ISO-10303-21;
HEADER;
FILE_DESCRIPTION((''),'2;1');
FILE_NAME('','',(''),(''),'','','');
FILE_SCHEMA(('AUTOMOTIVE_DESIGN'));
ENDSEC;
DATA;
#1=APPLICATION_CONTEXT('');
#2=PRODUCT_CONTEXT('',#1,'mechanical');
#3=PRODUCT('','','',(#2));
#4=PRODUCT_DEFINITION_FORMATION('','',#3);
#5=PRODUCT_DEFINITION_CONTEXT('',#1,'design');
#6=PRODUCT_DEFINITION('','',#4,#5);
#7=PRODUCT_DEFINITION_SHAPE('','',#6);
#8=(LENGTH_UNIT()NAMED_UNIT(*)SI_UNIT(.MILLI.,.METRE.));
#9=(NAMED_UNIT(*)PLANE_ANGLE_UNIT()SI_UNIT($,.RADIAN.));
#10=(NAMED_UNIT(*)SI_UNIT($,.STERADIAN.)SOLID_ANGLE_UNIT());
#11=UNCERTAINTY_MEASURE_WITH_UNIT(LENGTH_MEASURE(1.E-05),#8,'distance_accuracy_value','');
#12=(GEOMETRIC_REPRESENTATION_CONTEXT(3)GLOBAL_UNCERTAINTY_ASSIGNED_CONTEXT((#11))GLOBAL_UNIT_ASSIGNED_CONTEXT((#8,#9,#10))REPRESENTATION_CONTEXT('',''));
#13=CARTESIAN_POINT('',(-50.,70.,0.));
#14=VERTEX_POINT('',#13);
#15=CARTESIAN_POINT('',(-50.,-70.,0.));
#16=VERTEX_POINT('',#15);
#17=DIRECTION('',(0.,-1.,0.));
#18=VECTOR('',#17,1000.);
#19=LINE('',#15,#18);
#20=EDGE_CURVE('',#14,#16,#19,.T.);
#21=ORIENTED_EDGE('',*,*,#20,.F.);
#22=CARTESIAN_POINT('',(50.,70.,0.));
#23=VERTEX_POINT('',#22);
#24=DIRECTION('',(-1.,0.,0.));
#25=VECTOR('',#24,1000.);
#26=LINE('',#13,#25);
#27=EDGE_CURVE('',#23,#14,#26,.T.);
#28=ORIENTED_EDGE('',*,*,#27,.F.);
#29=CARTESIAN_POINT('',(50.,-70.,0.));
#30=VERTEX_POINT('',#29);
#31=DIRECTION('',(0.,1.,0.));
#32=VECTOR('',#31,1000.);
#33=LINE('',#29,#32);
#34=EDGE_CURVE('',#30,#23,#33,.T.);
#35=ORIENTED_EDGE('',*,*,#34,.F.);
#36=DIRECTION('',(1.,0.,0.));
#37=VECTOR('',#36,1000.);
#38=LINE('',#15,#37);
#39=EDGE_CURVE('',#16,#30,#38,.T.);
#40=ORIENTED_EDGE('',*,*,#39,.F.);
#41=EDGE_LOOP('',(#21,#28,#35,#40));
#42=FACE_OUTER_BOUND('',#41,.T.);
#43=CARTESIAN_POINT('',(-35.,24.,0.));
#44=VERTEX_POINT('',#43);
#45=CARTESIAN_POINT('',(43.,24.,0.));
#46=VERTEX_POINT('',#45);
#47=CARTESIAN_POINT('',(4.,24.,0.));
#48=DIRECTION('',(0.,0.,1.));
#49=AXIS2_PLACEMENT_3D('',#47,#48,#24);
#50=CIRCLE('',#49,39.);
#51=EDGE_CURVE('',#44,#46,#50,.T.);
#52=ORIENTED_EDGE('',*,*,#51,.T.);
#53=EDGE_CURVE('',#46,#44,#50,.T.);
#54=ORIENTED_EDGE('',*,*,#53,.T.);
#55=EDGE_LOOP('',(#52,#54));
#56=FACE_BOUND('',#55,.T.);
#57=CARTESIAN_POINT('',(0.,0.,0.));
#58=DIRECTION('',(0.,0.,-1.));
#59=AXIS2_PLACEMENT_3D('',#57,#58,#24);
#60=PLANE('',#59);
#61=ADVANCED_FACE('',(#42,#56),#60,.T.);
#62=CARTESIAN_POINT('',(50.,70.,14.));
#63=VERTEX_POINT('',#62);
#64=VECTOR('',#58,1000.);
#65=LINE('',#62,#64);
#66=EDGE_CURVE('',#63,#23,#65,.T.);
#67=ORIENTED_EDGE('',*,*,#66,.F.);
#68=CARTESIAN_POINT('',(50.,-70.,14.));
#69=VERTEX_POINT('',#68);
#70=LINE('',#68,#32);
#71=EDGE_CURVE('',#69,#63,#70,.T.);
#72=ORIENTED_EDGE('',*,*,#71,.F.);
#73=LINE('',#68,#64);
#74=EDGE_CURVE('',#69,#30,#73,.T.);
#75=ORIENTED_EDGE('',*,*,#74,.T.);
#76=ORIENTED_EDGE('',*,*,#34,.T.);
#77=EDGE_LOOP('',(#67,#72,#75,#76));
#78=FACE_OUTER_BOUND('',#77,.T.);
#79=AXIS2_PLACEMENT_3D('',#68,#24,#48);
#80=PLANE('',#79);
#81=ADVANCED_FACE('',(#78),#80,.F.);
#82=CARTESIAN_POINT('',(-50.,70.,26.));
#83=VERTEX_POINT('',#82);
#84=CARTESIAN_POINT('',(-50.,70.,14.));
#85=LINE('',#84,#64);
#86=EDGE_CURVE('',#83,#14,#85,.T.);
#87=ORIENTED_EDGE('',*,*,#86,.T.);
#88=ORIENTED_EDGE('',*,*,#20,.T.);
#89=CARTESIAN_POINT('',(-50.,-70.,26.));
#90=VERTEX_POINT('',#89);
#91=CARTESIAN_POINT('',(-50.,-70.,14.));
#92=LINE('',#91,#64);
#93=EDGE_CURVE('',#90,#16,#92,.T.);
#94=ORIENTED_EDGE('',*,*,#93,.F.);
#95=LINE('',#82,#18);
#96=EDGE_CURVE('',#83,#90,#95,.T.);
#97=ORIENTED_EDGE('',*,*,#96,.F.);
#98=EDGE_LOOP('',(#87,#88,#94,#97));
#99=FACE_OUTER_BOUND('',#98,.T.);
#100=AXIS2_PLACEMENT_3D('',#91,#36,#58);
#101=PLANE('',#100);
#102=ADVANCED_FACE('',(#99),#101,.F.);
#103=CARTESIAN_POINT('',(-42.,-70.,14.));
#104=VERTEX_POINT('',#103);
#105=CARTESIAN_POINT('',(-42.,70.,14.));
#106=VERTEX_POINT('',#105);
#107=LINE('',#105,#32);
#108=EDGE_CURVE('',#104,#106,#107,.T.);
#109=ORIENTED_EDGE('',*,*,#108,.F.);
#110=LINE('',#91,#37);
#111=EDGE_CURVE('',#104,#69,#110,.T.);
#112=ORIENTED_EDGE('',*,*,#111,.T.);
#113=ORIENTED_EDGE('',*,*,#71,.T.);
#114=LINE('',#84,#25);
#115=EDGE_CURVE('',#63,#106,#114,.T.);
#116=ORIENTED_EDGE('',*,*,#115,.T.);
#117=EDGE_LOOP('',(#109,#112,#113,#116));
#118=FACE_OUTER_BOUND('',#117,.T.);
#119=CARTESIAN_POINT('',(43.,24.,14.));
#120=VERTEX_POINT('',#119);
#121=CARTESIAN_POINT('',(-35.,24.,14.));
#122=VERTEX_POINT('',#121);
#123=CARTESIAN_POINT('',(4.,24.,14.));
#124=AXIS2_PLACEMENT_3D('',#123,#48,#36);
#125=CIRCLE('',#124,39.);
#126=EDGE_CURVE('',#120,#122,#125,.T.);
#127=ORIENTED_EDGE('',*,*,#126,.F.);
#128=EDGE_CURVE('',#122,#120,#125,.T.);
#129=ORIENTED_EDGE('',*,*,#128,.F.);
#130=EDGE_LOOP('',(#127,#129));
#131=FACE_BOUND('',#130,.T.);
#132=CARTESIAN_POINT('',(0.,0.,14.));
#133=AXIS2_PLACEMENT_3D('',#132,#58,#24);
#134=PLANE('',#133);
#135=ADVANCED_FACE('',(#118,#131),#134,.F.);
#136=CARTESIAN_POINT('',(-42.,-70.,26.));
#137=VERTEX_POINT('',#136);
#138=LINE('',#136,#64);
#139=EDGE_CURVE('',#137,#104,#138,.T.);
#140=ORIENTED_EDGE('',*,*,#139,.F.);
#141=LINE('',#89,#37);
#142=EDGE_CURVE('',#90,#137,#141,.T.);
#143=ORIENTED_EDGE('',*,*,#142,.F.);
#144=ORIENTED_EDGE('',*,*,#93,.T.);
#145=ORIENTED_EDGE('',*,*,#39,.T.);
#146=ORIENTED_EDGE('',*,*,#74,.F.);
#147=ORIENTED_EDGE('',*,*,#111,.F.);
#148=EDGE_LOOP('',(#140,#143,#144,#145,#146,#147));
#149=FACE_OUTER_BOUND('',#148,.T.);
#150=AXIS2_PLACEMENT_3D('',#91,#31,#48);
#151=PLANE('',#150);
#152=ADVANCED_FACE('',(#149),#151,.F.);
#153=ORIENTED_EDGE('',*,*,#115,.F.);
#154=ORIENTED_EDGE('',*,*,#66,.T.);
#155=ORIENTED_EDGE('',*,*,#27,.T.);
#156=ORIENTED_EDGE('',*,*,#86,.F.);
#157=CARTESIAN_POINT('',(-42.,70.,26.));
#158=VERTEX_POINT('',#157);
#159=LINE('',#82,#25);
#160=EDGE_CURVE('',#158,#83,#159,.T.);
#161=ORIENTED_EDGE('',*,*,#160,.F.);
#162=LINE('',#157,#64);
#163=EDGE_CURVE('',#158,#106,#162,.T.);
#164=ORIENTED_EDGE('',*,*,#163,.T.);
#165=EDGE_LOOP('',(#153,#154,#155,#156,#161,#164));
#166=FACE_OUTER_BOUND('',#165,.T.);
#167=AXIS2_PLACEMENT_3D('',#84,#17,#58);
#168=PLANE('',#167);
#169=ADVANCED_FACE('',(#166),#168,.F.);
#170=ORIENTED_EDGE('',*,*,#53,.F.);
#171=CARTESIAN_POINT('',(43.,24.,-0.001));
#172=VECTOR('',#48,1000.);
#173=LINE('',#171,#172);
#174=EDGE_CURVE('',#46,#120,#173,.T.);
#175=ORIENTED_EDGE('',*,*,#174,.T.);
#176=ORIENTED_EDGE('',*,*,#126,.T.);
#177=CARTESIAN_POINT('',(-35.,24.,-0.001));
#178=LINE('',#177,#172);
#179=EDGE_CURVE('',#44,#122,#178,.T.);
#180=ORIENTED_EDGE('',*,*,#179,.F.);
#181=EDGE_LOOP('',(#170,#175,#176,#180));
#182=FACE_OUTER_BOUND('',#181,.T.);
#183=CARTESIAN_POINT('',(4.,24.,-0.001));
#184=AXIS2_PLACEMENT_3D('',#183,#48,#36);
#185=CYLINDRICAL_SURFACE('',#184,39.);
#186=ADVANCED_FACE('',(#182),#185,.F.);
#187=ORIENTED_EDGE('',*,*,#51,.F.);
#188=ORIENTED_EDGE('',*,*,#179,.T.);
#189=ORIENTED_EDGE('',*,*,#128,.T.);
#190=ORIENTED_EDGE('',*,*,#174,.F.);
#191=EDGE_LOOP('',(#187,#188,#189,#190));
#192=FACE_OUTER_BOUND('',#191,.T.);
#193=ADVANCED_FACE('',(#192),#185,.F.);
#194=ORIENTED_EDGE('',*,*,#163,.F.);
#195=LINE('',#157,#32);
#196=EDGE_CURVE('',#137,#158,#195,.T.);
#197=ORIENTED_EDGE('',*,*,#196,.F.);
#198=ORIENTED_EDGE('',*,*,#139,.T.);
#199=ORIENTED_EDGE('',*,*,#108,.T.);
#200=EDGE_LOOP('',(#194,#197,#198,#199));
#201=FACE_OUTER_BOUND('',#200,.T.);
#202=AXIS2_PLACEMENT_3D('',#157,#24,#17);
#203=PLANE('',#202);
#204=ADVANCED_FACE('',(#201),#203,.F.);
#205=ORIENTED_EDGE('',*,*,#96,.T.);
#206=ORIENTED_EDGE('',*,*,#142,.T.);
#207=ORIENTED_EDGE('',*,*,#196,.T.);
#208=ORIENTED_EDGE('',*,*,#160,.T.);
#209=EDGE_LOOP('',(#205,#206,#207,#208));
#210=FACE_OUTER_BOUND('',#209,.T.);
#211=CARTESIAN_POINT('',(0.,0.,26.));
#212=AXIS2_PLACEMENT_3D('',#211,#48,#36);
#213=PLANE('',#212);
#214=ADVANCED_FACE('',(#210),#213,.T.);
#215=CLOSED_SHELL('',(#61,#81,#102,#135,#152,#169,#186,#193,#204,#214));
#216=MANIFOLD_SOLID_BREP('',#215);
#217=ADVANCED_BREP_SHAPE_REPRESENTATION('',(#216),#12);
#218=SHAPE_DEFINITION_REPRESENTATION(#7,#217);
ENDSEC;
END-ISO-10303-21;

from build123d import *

# Parameters (mm, degrees)
SKETCH_1_W          = 100
SKETCH_1_H          = 140
EXTRUDE_1_DEPTH     = 14
CUT_EXTRUDE_1_REACH = 89.155
SKETCH_2_R          = 39
SKETCH_3_W          = 8
SKETCH_3_H          = 140
EXTRUDE_2_DEPTH     = 12


with BuildPart() as part:
    # 草图1 → 凸台-拉伸1 (new body)
    with BuildSketch(Plane.XY):
        Rectangle(SKETCH_1_W, SKETCH_1_H)
    extrude(amount=EXTRUDE_1_DEPTH)

    # 草图2 → 切除-拉伸1 (cut, up to next)
    with BuildSketch(Plane.XY.offset(14), mode=Mode.PRIVATE) as cut_extrude_1_sk1:
        with Locations((4, 24)):
            Circle(SKETCH_2_R)
    cut_extrude_1_tool1 = extrude(cut_extrude_1_sk1.sketch, amount=-CUT_EXTRUDE_1_REACH, mode=Mode.PRIVATE) & part.part
    add(cut_extrude_1_tool1.solids().sort_by_distance((4, 24, 14))[0], mode=Mode.SUBTRACT)

    # 草图3 → 凸台-拉伸2 (add)
    with BuildSketch(Plane.XY.offset(14)):
        with Locations((-46, 0)):
            Rectangle(SKETCH_3_W, SKETCH_3_H)
    extrude(amount=EXTRUDE_2_DEPTH)


solid = part.part
